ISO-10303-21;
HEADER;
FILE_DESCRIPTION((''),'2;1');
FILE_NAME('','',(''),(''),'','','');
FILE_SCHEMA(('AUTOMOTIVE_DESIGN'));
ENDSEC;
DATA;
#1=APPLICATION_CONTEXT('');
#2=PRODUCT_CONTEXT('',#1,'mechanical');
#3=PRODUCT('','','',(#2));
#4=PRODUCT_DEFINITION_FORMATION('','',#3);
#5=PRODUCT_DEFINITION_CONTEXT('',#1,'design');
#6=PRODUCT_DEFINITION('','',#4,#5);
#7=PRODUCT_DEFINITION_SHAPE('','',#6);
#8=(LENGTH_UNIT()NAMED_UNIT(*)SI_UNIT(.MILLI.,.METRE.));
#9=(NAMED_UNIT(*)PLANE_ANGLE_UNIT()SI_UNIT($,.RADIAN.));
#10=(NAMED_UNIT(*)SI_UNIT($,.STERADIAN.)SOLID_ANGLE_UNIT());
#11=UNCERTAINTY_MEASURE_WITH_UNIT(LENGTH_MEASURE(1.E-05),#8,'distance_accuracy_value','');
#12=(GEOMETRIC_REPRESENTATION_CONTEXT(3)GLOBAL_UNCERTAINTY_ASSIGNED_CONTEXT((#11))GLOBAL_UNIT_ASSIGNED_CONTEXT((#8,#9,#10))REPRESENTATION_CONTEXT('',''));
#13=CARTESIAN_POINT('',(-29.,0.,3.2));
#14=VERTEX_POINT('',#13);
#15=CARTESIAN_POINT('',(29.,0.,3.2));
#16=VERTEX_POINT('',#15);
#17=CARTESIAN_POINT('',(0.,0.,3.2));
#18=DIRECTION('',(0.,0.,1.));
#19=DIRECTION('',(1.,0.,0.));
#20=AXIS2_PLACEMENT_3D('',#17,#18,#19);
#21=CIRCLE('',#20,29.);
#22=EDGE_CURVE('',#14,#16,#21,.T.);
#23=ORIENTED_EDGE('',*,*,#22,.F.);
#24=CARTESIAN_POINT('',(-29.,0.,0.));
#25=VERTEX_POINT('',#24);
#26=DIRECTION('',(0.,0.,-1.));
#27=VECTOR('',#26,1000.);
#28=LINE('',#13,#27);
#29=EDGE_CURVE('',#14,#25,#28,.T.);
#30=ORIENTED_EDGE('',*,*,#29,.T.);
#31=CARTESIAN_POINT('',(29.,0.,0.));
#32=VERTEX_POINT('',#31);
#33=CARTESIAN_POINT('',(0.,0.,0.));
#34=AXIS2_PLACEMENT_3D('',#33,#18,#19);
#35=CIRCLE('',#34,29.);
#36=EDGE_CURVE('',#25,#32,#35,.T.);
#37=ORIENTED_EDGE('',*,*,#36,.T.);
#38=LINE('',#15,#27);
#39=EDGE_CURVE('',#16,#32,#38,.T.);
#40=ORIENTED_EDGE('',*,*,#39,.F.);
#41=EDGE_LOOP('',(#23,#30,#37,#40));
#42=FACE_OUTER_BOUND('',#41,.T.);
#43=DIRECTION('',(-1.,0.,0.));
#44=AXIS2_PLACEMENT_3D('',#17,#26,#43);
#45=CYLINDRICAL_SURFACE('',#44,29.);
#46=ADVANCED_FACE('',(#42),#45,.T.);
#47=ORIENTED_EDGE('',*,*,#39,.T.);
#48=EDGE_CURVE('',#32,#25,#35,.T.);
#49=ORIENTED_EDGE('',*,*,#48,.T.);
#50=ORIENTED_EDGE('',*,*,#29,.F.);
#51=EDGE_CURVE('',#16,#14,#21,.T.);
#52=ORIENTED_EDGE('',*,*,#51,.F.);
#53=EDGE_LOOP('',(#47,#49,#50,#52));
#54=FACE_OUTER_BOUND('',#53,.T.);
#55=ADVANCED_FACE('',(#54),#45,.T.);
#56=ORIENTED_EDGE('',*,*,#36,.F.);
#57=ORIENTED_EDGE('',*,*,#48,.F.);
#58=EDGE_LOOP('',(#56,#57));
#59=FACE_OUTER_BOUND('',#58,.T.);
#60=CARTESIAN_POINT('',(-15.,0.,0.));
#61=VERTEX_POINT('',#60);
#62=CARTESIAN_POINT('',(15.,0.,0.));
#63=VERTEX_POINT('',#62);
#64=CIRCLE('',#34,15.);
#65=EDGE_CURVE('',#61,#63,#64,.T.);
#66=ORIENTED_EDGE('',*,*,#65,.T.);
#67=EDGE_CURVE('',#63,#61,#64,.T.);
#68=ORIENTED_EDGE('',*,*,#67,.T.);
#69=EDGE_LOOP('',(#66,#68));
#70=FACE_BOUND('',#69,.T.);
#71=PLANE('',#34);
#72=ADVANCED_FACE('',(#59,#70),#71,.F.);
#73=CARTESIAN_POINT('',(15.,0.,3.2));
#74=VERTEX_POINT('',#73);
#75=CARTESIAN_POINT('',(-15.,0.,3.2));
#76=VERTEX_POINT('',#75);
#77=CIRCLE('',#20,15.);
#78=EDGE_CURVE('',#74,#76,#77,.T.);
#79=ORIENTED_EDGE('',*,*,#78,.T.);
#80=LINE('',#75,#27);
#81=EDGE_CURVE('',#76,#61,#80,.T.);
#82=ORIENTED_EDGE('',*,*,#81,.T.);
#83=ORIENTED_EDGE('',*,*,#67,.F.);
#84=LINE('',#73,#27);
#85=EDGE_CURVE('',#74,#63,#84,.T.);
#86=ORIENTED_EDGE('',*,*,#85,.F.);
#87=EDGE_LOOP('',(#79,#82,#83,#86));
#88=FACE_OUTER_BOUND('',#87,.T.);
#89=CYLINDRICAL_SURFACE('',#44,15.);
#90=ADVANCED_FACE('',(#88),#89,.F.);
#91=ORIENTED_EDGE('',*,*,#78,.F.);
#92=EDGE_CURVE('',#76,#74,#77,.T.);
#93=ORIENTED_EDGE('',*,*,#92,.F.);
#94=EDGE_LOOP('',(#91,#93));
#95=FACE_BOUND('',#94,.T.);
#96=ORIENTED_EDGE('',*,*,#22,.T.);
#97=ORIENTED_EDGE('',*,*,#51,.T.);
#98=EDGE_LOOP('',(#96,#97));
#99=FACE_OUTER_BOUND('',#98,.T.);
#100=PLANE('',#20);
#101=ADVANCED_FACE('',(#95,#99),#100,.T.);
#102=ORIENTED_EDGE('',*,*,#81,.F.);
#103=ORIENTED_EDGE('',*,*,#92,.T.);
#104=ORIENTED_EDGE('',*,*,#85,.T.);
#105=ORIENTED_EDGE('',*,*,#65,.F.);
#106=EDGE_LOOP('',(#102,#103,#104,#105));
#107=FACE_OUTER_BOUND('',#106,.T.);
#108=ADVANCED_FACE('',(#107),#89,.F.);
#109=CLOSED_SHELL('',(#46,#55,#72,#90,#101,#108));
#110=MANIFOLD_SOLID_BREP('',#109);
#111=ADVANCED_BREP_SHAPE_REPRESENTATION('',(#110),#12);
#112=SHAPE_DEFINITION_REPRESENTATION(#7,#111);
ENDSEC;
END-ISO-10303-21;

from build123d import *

# Parameters (mm, degrees)
SKETCH_1_R      = 29
SKETCH_1_R_2    = 15
EXTRUDE_1_DEPTH = 3.2


with BuildPart() as part:
    # 草图1 → 凸台-拉伸1 (new body)
    with BuildSketch(Plane.XY):
        Circle(SKETCH_1_R)
        Circle(SKETCH_1_R_2, mode=Mode.SUBTRACT)
    extrude(amount=EXTRUDE_1_DEPTH)


solid = part.part
